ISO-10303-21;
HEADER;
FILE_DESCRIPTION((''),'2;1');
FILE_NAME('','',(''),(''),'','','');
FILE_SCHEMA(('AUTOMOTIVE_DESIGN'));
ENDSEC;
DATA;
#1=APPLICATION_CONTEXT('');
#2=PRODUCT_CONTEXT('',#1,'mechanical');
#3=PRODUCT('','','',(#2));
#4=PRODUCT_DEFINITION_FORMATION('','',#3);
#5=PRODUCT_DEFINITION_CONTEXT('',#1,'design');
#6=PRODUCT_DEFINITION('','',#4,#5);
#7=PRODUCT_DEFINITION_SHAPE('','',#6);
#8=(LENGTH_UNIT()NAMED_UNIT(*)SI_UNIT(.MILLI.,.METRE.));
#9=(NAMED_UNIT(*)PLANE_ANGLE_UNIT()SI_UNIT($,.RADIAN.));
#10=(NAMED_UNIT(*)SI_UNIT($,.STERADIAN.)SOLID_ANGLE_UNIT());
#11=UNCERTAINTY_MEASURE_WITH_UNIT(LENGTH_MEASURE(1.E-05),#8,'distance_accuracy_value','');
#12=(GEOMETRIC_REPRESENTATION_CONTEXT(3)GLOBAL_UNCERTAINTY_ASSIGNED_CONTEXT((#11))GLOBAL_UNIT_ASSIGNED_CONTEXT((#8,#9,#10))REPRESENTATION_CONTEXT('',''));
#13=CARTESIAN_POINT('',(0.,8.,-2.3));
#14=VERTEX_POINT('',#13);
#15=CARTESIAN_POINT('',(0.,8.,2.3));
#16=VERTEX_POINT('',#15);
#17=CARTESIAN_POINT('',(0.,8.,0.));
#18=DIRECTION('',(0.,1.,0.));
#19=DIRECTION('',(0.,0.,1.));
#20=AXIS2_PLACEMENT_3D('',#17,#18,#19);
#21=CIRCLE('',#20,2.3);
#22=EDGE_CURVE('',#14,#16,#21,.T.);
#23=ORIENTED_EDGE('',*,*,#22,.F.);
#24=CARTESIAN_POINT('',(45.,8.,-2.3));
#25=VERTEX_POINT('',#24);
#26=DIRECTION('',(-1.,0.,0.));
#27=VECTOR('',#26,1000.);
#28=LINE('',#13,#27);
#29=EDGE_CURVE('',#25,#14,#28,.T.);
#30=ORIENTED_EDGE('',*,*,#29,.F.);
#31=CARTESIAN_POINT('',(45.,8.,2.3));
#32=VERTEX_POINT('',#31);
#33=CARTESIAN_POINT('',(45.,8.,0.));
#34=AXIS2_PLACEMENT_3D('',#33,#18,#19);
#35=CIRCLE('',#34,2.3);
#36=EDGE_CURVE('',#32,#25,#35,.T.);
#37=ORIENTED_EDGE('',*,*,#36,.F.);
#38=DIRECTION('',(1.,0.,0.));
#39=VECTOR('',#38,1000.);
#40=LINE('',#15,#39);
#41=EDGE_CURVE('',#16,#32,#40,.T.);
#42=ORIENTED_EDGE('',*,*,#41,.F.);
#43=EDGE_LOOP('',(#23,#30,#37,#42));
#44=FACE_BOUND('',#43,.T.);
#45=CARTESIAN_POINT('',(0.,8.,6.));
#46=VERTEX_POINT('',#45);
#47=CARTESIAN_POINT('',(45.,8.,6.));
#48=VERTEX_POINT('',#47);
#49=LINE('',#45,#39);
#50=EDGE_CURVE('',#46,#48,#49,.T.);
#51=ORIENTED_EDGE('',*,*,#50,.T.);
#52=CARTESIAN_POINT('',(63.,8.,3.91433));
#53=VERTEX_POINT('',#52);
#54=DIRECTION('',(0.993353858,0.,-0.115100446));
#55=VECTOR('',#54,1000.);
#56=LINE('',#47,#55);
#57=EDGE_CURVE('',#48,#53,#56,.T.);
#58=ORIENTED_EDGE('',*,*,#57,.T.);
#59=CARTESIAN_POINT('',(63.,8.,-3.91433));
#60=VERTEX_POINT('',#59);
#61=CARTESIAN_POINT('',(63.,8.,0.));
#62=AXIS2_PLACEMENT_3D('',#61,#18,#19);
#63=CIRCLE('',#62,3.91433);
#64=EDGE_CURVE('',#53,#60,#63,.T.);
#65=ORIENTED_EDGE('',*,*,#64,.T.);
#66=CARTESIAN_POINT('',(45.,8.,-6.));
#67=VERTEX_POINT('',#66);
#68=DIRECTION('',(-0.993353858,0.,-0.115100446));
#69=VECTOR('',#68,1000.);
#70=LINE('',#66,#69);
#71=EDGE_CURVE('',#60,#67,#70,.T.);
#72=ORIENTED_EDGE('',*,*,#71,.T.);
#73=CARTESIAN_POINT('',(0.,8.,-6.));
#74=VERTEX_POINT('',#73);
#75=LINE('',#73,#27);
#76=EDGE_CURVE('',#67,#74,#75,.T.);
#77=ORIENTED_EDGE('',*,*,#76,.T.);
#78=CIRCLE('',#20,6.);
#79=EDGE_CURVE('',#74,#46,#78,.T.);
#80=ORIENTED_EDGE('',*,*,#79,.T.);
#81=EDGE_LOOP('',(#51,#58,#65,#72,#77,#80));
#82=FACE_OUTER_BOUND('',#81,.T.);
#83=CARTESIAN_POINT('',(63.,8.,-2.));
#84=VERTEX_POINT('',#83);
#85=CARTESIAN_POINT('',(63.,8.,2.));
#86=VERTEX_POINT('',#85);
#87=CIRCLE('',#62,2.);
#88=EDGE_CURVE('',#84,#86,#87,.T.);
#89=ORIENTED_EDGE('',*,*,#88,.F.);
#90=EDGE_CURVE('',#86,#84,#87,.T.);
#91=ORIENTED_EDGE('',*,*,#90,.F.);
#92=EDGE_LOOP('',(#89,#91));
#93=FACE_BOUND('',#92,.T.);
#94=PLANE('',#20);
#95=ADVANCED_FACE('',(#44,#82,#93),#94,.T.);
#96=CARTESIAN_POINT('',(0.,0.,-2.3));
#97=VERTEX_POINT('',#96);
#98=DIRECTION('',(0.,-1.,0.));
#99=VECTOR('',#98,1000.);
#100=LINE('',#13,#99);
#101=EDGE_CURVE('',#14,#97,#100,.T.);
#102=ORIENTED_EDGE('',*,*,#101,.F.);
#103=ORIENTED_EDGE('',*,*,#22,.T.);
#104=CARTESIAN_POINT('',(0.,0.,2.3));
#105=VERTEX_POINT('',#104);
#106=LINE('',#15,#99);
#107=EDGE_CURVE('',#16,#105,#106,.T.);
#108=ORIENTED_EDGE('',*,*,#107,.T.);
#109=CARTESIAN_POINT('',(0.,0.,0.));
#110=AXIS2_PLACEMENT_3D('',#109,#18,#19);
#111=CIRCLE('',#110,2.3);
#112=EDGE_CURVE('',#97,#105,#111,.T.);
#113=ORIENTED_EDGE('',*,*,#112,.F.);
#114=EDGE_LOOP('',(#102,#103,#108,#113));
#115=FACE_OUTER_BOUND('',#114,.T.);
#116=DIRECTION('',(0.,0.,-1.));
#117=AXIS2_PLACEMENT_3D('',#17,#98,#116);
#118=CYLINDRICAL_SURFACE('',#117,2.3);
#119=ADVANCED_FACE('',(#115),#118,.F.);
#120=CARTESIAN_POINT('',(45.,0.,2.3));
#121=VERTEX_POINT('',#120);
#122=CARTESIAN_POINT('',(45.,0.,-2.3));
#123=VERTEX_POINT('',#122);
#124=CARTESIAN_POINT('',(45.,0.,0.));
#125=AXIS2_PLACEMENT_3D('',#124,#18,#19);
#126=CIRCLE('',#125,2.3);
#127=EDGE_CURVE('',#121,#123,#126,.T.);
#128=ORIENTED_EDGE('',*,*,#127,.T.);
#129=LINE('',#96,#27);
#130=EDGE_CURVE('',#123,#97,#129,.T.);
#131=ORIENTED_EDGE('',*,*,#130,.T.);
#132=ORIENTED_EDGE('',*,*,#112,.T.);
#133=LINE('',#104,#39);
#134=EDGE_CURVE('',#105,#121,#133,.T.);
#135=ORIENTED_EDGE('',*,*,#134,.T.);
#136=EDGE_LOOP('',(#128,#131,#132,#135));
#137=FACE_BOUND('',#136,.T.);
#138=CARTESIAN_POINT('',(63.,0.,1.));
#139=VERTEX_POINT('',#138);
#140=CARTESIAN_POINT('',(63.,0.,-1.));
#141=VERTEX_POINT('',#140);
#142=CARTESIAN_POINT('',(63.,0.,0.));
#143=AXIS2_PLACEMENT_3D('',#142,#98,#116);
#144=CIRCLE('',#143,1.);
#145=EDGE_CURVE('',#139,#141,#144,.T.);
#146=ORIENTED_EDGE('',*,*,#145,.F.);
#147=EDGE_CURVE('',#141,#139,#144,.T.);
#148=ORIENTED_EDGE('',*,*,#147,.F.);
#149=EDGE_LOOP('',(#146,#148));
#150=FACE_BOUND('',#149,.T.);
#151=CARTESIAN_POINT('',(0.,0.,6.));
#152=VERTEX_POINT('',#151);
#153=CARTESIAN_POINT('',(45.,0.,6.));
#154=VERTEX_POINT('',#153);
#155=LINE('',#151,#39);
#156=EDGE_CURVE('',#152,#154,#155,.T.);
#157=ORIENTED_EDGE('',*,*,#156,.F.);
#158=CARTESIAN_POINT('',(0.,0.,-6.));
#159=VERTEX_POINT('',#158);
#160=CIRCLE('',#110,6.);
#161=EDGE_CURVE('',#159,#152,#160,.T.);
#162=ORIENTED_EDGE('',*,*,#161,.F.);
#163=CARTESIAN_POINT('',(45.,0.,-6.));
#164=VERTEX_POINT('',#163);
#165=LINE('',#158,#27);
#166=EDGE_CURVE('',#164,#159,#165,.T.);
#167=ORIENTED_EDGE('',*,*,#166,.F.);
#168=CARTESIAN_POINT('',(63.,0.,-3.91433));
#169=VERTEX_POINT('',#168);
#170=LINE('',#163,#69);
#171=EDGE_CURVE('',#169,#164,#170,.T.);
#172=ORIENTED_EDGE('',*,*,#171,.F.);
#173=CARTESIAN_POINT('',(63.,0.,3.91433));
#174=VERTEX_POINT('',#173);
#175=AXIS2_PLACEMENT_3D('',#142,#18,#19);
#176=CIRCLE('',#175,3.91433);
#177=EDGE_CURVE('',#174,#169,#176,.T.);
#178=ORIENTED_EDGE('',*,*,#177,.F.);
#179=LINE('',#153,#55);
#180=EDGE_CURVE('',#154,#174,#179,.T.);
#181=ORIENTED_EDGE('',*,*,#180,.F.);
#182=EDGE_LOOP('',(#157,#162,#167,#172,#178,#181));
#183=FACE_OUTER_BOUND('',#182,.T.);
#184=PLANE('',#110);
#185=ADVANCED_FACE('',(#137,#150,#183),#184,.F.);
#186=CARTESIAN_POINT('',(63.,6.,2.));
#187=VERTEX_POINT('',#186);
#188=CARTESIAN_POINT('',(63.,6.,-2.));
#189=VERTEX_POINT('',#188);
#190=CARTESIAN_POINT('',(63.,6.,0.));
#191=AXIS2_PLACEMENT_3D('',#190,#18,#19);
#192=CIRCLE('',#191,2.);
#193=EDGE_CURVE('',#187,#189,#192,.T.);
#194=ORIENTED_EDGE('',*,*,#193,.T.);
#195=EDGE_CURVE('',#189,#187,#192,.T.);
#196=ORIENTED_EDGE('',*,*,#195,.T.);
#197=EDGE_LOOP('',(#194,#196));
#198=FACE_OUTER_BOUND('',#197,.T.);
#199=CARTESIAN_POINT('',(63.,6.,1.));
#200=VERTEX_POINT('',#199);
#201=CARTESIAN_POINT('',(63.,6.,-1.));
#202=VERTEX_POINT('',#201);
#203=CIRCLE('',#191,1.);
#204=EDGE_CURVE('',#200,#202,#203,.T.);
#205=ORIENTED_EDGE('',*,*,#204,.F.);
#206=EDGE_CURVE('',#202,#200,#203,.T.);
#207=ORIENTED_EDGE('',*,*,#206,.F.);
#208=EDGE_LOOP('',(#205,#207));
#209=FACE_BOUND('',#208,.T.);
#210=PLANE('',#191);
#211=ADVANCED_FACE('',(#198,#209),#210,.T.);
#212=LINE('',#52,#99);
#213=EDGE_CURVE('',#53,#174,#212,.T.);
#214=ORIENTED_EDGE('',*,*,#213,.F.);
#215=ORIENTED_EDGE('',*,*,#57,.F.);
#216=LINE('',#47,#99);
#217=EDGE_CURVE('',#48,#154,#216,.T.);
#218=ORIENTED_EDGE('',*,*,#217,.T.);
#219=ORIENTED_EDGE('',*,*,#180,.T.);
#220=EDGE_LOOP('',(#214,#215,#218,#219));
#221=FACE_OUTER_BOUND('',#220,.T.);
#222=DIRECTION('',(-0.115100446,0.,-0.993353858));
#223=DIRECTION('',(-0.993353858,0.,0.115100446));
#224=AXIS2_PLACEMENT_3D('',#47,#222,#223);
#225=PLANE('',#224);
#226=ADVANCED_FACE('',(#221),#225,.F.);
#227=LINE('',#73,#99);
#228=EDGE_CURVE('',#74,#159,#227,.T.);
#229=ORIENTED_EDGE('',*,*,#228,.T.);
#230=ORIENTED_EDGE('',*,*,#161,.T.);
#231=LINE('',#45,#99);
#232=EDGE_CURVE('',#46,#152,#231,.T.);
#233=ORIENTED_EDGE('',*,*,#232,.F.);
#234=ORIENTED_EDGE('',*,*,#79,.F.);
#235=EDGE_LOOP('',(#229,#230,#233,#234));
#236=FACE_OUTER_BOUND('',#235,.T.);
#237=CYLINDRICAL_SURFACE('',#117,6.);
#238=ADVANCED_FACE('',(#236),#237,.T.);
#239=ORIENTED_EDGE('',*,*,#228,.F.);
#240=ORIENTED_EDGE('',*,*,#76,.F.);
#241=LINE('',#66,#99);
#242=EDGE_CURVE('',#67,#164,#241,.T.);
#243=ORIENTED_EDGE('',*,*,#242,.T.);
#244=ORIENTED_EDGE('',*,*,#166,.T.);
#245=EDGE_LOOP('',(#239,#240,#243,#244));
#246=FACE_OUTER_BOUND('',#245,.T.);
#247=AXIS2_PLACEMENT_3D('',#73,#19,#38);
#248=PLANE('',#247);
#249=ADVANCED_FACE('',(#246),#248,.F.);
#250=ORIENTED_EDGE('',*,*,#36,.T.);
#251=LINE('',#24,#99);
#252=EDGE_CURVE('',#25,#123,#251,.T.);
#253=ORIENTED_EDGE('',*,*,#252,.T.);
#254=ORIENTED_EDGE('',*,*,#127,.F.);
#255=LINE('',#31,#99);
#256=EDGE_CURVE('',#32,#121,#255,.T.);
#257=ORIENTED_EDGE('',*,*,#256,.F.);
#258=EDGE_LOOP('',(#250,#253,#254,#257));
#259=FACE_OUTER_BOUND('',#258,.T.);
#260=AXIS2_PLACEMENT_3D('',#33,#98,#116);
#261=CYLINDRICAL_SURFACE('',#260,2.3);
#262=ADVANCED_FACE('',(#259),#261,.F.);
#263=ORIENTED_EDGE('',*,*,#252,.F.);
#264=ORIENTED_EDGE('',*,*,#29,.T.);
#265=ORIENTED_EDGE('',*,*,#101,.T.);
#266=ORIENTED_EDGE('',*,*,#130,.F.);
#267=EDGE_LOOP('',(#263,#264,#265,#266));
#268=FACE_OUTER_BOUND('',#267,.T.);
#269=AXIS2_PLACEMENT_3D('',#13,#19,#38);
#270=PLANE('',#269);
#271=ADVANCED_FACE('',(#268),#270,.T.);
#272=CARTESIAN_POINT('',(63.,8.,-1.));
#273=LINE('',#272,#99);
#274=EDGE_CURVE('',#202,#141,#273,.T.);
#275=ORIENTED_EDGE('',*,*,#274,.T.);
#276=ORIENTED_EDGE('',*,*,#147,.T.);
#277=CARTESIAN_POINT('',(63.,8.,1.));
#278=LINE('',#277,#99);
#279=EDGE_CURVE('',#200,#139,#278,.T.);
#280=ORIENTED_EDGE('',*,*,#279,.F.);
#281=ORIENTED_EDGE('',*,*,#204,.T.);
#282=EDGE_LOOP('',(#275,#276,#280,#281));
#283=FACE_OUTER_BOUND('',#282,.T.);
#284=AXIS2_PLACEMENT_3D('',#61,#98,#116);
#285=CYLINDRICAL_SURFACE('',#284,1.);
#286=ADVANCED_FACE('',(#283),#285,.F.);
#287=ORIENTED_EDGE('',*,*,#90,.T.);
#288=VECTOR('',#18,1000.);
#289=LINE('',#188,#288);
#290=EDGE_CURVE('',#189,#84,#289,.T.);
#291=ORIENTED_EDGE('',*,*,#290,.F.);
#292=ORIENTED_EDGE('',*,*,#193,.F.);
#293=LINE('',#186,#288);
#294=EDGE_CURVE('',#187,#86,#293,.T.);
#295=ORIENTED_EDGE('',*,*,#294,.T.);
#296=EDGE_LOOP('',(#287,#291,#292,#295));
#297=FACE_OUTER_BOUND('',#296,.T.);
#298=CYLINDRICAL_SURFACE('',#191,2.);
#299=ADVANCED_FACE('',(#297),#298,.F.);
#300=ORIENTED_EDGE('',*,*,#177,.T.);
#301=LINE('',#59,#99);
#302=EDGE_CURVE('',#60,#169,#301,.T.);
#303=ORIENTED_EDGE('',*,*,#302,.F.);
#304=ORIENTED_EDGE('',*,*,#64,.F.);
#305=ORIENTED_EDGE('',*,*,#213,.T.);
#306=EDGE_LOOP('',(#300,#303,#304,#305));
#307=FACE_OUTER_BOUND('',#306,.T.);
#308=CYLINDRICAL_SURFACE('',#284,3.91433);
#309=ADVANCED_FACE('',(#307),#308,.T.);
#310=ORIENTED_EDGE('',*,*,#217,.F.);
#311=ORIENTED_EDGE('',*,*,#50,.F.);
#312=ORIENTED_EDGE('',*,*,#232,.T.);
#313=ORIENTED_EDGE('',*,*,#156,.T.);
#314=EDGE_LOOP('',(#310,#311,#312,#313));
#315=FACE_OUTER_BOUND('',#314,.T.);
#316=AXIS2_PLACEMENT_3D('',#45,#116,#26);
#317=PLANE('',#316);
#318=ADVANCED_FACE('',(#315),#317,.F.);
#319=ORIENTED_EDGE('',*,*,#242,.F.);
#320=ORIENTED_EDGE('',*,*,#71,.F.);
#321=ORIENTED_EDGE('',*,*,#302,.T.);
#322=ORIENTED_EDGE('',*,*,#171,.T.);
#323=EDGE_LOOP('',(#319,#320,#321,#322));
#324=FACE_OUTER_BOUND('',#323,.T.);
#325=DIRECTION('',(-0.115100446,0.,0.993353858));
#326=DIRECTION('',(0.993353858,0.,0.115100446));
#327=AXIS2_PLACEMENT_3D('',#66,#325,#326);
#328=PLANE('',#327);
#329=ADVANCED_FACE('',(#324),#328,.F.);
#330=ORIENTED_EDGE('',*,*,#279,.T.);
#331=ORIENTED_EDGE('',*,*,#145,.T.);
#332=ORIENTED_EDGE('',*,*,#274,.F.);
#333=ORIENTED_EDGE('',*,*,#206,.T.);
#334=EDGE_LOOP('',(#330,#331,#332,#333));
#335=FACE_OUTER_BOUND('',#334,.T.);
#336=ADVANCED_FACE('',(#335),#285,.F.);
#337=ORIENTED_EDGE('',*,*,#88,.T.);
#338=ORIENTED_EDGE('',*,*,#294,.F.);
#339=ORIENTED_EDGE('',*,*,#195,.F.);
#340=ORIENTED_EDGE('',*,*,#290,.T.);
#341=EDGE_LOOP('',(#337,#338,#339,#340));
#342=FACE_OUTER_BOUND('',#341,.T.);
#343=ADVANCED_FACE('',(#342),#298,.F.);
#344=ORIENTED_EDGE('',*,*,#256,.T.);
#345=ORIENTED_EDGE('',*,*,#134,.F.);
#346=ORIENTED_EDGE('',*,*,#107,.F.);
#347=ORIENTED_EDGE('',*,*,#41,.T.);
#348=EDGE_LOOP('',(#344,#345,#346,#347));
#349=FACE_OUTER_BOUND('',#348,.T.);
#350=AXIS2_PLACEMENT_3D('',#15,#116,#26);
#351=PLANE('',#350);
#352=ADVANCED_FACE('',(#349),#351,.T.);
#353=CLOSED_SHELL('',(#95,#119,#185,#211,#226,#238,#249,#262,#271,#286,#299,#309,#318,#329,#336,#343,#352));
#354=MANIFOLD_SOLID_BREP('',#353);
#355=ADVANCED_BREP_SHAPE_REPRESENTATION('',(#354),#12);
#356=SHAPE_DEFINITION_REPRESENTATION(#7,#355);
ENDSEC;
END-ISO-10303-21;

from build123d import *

# Parameters (mm, degrees)
BOSS_EXTRUDE1_DEPTH = 8
SKETCH2_R           = 2
CUT_EXTRUDE1_DEPTH  = 2
SKETCH3_R           = 1
CUT_EXTRUDE2_DEPTH  = 68.657428272


with BuildPart() as part:
    # Sketch1 → Boss-Extrude1 (new body)
    with BuildSketch(Plane(origin=(0, 0, 0), x_dir=(1, 0, 0), z_dir=(0, 1, 0))):
        with BuildLine():
            Line((0, 6), (45, 6))
            Line((45, 6), (63, 3.914330307))
            ThreePointArc((63, 3.914330307), (66.914330307, 0), (63, -3.914330307))
            Line((63, -3.914330307), (45, -6))
            Line((45, -6), (0, -6))
            ThreePointArc((0, -6), (-6, 0), (0, 6))
        make_face()
        with BuildLine():
            Line((0, 2.3), (45, 2.3))
            ThreePointArc((45, 2.3), (47.3, 0), (45, -2.3))
            Line((45, -2.3), (0, -2.3))
            ThreePointArc((0, -2.3), (-2.3, 0), (0, 2.3))
        make_face(mode=Mode.SUBTRACT)
    extrude(amount=BOSS_EXTRUDE1_DEPTH)

    # Sketch2 → Cut-Extrude1 (cut)
    with BuildSketch(Plane(origin=(0, 8, 0), x_dir=(1, 0, 0), z_dir=(0, 1, 0))):
        with Locations(Location((63, 0, 0), (0, 0, 270))):
            Circle(SKETCH2_R)
    extrude(amount=-CUT_EXTRUDE1_DEPTH, mode=Mode.SUBTRACT)

    # Sketch3 → Cut-Extrude2 (cut, through all)
    with BuildSketch(Plane.XZ):
        with Locations(Location((63, 0, 0), (0, 0, 270))):
            Circle(SKETCH3_R)
    extrude(amount=-CUT_EXTRUDE2_DEPTH, mode=Mode.SUBTRACT)


solid = part.part
